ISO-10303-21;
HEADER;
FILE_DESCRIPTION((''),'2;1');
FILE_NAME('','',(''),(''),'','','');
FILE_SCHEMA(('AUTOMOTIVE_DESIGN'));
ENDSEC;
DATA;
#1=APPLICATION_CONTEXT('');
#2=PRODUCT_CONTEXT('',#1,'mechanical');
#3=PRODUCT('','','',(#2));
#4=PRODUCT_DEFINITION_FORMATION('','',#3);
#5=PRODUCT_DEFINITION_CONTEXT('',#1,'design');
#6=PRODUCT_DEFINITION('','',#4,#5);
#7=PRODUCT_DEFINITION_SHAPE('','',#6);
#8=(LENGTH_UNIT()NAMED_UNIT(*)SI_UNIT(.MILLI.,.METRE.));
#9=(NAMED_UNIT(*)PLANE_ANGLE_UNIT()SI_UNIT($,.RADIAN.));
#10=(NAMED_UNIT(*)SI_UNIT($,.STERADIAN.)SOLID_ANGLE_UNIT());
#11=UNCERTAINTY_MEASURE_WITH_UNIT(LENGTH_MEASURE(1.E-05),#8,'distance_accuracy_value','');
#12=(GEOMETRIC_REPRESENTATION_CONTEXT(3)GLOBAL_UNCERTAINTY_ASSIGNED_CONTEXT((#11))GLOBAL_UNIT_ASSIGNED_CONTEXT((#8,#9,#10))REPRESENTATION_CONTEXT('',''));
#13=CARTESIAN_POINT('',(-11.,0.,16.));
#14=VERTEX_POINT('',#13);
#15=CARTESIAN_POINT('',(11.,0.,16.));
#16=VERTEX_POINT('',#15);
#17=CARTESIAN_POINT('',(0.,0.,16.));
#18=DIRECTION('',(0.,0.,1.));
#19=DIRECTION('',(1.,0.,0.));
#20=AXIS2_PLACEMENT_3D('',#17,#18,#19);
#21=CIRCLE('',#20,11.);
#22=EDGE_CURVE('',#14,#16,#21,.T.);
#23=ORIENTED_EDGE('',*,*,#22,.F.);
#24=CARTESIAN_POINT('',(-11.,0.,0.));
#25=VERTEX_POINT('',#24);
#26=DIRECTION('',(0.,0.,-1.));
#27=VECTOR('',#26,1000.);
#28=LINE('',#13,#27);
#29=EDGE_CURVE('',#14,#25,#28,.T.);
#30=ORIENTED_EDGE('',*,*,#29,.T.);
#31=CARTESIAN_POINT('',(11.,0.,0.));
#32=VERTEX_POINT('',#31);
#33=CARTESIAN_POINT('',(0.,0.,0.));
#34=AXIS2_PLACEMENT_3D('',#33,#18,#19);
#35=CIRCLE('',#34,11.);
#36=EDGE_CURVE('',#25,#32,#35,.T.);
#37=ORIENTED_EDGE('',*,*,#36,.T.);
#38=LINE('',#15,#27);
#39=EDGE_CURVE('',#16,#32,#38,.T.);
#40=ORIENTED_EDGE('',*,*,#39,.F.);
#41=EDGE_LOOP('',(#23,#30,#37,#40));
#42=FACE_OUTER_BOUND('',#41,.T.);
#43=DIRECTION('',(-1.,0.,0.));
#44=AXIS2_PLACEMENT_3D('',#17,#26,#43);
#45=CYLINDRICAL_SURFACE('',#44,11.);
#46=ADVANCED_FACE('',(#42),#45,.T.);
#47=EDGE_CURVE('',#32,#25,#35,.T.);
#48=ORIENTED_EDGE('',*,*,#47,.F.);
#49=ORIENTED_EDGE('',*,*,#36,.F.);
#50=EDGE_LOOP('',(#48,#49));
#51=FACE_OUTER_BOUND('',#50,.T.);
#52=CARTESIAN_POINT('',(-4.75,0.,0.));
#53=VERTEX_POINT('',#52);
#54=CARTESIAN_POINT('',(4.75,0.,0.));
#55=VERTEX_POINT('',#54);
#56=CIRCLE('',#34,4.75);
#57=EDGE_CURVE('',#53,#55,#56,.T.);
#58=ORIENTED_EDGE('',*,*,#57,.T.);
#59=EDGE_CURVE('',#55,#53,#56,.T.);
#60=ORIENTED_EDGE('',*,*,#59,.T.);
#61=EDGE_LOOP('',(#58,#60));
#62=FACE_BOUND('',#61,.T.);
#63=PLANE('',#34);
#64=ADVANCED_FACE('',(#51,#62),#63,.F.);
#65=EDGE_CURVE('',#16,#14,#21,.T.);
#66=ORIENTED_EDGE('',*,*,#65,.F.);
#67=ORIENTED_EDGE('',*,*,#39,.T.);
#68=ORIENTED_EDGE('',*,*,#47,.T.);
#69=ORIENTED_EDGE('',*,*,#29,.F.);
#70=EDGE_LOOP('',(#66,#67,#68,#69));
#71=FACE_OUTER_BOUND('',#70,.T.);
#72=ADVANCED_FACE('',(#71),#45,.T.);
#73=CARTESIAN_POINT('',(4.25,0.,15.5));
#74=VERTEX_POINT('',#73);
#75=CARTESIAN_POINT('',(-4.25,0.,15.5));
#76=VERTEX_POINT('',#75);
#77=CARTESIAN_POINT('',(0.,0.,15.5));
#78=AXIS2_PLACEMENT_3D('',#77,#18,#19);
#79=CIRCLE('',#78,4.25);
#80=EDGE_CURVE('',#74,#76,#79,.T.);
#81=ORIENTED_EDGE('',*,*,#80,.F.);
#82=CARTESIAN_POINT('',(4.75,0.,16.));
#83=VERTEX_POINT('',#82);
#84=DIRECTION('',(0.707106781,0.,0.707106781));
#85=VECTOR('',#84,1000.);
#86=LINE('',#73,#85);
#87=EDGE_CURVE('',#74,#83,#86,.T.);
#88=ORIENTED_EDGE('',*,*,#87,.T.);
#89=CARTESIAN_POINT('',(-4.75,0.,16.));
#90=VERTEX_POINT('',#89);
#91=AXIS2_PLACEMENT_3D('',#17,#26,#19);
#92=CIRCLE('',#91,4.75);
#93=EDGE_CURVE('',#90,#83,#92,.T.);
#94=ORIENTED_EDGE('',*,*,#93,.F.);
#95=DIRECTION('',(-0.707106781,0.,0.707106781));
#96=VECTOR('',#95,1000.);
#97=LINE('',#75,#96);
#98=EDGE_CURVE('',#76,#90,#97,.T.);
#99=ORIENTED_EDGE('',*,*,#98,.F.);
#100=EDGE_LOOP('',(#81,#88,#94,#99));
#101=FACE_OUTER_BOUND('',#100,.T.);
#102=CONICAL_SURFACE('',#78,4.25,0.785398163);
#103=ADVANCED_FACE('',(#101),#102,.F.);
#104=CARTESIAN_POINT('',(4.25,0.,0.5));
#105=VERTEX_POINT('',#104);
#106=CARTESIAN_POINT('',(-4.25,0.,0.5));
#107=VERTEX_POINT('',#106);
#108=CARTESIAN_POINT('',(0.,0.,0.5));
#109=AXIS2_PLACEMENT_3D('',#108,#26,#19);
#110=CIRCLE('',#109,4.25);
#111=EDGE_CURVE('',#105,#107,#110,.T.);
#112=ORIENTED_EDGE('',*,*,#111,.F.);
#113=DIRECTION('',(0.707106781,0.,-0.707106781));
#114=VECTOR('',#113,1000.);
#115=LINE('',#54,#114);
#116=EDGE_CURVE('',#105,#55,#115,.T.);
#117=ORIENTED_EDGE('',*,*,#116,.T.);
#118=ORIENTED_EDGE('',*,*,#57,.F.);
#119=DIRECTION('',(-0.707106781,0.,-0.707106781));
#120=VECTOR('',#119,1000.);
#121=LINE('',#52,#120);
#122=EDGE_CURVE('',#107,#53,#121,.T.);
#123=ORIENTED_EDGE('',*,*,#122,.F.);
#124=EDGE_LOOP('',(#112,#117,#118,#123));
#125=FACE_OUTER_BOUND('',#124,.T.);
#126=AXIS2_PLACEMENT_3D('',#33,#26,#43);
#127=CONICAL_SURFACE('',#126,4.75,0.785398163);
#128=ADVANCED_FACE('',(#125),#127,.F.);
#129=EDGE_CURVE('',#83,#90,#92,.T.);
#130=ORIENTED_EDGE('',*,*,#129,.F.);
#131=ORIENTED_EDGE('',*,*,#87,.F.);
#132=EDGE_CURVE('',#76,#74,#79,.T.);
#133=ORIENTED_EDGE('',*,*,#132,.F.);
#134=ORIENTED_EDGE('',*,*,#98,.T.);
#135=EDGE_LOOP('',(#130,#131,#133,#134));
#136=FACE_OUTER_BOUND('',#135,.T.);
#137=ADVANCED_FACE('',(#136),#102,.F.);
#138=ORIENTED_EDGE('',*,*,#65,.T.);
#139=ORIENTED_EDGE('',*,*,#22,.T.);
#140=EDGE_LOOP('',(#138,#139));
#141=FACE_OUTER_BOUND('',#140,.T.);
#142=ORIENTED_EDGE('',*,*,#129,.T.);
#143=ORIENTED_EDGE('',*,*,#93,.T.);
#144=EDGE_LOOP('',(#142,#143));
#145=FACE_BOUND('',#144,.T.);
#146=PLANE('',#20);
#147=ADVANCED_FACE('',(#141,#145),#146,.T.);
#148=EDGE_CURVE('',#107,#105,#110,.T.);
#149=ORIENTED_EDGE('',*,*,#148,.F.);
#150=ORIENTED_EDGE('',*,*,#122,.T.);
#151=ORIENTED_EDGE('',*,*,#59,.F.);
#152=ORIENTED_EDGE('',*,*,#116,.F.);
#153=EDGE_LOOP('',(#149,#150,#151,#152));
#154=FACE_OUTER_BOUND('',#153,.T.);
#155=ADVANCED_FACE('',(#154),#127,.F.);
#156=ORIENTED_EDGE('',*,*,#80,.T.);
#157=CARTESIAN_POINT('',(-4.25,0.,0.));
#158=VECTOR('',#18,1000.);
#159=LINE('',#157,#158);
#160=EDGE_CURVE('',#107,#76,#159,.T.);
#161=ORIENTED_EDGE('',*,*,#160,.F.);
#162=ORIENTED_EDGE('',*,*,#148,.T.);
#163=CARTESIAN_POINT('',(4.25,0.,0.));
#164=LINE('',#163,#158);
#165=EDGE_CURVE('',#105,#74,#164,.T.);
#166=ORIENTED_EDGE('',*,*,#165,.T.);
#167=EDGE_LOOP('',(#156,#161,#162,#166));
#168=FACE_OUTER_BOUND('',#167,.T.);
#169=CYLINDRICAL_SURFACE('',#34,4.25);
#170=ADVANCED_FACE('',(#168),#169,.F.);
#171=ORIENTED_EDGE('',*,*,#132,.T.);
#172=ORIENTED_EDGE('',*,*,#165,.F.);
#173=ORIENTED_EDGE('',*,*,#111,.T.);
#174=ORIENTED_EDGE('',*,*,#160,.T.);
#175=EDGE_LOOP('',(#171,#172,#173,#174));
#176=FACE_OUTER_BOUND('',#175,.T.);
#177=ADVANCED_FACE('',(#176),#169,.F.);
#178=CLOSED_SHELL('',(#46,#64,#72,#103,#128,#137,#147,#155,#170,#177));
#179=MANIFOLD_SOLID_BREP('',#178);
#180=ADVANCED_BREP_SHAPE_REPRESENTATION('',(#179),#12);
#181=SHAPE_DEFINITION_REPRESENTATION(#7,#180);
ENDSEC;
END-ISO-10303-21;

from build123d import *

# Parameters (mm, degrees)
SKETCH1_R           = 11
BOSS_EXTRUDE1_DEPTH = 16
SKETCH2_R           = 4.25
CUT_EXTRUDE1_DEPTH  = 16
CHAMFER1_SIZE       = 0.5


with BuildPart() as part:
    # Sketch1 → Boss-Extrude1 (new body)
    with BuildSketch(Plane.XY):
        Circle(SKETCH1_R)
    extrude(amount=BOSS_EXTRUDE1_DEPTH)

    # Sketch2 → Cut-Extrude1 (cut)
    with BuildSketch(Plane.XY.offset(16)):
        Circle(SKETCH2_R)
    extrude(amount=-CUT_EXTRUDE1_DEPTH, mode=Mode.SUBTRACT)

    # Chamfer1
    chamfer1_edges = [part.edges().sort_by_distance(p)[0] for p in [
        (-4.25, 0, 0),
        (-4.25, 0, 16),
    ]]
    chamfer(chamfer1_edges, length=CHAMFER1_SIZE)


solid = part.part
